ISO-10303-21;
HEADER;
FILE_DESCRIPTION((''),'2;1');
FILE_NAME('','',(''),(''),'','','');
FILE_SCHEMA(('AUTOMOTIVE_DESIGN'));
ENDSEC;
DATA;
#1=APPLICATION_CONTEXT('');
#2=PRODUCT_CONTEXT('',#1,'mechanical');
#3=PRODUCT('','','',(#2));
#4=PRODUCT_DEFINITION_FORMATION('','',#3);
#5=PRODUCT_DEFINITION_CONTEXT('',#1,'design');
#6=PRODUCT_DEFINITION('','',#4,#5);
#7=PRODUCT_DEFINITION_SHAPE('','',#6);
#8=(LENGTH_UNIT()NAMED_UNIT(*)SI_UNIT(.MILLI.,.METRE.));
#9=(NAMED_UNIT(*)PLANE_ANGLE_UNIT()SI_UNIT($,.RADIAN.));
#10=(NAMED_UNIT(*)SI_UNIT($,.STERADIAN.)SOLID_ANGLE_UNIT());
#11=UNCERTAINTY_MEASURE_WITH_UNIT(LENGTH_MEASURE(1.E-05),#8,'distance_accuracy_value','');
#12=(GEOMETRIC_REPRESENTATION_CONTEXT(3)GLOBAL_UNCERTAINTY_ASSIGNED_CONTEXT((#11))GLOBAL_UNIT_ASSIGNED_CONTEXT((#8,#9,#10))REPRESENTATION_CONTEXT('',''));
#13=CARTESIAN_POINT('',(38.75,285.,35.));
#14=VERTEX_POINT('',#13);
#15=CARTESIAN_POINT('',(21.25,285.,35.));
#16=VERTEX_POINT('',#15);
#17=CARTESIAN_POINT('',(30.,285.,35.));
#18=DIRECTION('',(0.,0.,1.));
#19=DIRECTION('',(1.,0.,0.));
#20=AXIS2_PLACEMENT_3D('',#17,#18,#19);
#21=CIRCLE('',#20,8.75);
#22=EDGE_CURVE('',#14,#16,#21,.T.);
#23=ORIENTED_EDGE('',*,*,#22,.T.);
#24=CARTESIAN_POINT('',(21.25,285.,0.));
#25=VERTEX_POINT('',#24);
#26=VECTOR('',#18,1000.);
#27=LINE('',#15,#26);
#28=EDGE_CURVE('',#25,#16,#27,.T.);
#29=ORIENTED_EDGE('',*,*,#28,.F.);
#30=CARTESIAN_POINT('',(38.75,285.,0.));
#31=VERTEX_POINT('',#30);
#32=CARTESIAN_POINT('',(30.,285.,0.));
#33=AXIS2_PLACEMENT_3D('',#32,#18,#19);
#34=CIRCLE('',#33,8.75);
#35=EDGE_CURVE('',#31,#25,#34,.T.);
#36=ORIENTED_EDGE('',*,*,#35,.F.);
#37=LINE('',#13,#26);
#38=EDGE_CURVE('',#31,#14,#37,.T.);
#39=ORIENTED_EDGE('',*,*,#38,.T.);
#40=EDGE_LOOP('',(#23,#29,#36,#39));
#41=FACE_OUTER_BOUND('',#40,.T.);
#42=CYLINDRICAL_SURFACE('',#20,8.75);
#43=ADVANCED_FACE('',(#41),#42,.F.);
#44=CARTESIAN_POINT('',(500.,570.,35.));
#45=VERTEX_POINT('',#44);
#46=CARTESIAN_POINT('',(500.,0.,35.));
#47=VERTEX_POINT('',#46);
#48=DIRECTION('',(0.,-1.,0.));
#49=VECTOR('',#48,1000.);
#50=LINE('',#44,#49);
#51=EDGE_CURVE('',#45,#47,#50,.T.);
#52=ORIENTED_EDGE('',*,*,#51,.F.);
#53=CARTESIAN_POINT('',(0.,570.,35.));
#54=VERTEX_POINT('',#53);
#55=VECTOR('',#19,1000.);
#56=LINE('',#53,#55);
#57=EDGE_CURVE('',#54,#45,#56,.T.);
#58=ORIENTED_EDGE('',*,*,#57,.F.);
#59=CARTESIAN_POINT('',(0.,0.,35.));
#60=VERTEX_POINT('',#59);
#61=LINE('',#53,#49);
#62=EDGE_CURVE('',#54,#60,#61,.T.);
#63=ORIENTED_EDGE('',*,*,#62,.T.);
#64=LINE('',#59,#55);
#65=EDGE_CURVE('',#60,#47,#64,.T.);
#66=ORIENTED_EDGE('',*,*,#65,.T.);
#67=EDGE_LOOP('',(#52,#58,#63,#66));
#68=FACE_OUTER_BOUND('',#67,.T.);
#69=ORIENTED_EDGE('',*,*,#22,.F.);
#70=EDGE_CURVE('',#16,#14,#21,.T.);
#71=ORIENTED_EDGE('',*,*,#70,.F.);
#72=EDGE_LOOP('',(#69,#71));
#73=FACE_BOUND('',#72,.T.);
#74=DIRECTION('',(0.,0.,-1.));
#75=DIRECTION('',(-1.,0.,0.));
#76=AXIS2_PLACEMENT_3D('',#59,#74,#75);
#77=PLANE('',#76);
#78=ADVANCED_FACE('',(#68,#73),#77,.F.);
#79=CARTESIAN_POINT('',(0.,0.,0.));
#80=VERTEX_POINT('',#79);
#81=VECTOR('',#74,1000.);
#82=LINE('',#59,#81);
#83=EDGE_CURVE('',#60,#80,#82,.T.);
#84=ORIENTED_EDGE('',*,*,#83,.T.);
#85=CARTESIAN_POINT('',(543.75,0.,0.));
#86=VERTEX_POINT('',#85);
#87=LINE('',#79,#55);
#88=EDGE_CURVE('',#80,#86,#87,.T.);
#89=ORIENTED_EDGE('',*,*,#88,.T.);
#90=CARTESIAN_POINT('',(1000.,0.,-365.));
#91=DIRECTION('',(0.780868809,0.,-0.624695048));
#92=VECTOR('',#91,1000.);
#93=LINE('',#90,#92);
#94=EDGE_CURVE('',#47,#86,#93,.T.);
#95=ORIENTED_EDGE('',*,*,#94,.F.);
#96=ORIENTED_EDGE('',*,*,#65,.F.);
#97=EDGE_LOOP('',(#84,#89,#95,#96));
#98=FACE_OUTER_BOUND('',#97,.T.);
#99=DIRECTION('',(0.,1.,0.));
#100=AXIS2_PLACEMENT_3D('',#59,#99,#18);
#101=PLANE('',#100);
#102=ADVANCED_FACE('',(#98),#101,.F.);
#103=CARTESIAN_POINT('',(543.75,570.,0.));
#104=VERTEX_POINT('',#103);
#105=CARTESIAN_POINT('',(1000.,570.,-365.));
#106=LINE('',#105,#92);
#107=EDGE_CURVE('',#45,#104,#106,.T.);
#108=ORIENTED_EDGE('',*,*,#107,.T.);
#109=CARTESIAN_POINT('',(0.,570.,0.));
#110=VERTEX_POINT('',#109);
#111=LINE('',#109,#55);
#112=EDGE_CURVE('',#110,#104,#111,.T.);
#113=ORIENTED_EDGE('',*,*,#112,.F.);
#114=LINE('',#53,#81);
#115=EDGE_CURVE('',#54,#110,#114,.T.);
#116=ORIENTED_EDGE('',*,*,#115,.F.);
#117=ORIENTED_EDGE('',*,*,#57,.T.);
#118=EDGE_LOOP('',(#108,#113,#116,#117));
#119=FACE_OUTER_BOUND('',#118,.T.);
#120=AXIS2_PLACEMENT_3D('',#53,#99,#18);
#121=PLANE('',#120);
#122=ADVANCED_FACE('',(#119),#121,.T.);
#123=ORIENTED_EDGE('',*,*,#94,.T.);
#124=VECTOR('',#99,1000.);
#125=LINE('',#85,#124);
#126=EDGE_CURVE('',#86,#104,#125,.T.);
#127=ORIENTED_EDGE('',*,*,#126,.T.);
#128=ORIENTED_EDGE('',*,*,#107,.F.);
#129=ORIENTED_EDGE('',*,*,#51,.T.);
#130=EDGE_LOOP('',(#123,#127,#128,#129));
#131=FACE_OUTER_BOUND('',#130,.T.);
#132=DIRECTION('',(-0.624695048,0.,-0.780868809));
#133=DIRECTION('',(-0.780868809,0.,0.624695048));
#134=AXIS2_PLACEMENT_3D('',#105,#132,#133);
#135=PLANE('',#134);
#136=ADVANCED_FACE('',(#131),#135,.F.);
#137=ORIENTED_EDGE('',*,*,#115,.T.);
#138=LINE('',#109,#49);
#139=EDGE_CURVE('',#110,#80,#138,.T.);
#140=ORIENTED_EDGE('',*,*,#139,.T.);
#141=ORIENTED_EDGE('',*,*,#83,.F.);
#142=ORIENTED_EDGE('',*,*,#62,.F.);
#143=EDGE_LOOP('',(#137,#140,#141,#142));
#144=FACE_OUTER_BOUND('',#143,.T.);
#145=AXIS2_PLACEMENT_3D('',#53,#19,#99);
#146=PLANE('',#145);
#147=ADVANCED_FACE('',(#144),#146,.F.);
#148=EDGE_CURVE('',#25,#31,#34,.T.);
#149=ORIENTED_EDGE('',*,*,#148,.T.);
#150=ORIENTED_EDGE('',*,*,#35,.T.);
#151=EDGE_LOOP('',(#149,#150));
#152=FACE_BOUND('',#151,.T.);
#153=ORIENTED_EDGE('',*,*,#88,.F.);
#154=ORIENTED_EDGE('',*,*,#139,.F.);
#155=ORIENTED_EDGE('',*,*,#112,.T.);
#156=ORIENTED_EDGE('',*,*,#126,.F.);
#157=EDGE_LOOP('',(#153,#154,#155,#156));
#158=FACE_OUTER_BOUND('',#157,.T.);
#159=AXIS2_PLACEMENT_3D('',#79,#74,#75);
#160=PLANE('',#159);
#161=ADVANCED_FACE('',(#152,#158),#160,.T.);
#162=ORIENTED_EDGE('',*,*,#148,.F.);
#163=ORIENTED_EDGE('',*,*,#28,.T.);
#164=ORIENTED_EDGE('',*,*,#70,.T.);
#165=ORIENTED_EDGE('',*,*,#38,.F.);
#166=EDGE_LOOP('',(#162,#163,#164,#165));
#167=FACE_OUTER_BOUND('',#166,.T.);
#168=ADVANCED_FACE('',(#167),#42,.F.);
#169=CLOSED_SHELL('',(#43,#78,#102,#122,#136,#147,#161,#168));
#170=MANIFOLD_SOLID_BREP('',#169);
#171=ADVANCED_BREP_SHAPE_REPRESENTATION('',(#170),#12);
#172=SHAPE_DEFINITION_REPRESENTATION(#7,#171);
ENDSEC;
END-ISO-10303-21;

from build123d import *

# Parameters (mm, degrees)
SKETCH1_W           = 1000
SKETCH1_H           = 570
BOSS_EXTRUDE1_DEPTH = 35
M20_TAPPED_HOLE1_D  = 17.5
CUT_EXTRUDE2_DEPTH  = 1152.575008412


with BuildPart() as part:
    # Sketch1 → Boss-Extrude1 (new body)
    with BuildSketch(Plane.XY):
        with Locations((500, 285)):
            Rectangle(SKETCH1_W, SKETCH1_H)
    extrude(amount=BOSS_EXTRUDE1_DEPTH)

    # M20 Tapped Hole1 (through all)
    with Locations(Plane(origin=(30, 285, 35), x_dir=(1, 0, 0), z_dir=(0, 0, 1))):
        with Locations((0, 0)):
            Hole(M20_TAPPED_HOLE1_D / 2)

    # Sketch4 → Cut-Extrude2 (cut, through all)
    with BuildSketch(Plane.XZ):
        Polygon((500, 35), (1000, 35), (1000, -365), align=None)
    extrude(amount=-CUT_EXTRUDE2_DEPTH, mode=Mode.SUBTRACT)


solid = part.part
